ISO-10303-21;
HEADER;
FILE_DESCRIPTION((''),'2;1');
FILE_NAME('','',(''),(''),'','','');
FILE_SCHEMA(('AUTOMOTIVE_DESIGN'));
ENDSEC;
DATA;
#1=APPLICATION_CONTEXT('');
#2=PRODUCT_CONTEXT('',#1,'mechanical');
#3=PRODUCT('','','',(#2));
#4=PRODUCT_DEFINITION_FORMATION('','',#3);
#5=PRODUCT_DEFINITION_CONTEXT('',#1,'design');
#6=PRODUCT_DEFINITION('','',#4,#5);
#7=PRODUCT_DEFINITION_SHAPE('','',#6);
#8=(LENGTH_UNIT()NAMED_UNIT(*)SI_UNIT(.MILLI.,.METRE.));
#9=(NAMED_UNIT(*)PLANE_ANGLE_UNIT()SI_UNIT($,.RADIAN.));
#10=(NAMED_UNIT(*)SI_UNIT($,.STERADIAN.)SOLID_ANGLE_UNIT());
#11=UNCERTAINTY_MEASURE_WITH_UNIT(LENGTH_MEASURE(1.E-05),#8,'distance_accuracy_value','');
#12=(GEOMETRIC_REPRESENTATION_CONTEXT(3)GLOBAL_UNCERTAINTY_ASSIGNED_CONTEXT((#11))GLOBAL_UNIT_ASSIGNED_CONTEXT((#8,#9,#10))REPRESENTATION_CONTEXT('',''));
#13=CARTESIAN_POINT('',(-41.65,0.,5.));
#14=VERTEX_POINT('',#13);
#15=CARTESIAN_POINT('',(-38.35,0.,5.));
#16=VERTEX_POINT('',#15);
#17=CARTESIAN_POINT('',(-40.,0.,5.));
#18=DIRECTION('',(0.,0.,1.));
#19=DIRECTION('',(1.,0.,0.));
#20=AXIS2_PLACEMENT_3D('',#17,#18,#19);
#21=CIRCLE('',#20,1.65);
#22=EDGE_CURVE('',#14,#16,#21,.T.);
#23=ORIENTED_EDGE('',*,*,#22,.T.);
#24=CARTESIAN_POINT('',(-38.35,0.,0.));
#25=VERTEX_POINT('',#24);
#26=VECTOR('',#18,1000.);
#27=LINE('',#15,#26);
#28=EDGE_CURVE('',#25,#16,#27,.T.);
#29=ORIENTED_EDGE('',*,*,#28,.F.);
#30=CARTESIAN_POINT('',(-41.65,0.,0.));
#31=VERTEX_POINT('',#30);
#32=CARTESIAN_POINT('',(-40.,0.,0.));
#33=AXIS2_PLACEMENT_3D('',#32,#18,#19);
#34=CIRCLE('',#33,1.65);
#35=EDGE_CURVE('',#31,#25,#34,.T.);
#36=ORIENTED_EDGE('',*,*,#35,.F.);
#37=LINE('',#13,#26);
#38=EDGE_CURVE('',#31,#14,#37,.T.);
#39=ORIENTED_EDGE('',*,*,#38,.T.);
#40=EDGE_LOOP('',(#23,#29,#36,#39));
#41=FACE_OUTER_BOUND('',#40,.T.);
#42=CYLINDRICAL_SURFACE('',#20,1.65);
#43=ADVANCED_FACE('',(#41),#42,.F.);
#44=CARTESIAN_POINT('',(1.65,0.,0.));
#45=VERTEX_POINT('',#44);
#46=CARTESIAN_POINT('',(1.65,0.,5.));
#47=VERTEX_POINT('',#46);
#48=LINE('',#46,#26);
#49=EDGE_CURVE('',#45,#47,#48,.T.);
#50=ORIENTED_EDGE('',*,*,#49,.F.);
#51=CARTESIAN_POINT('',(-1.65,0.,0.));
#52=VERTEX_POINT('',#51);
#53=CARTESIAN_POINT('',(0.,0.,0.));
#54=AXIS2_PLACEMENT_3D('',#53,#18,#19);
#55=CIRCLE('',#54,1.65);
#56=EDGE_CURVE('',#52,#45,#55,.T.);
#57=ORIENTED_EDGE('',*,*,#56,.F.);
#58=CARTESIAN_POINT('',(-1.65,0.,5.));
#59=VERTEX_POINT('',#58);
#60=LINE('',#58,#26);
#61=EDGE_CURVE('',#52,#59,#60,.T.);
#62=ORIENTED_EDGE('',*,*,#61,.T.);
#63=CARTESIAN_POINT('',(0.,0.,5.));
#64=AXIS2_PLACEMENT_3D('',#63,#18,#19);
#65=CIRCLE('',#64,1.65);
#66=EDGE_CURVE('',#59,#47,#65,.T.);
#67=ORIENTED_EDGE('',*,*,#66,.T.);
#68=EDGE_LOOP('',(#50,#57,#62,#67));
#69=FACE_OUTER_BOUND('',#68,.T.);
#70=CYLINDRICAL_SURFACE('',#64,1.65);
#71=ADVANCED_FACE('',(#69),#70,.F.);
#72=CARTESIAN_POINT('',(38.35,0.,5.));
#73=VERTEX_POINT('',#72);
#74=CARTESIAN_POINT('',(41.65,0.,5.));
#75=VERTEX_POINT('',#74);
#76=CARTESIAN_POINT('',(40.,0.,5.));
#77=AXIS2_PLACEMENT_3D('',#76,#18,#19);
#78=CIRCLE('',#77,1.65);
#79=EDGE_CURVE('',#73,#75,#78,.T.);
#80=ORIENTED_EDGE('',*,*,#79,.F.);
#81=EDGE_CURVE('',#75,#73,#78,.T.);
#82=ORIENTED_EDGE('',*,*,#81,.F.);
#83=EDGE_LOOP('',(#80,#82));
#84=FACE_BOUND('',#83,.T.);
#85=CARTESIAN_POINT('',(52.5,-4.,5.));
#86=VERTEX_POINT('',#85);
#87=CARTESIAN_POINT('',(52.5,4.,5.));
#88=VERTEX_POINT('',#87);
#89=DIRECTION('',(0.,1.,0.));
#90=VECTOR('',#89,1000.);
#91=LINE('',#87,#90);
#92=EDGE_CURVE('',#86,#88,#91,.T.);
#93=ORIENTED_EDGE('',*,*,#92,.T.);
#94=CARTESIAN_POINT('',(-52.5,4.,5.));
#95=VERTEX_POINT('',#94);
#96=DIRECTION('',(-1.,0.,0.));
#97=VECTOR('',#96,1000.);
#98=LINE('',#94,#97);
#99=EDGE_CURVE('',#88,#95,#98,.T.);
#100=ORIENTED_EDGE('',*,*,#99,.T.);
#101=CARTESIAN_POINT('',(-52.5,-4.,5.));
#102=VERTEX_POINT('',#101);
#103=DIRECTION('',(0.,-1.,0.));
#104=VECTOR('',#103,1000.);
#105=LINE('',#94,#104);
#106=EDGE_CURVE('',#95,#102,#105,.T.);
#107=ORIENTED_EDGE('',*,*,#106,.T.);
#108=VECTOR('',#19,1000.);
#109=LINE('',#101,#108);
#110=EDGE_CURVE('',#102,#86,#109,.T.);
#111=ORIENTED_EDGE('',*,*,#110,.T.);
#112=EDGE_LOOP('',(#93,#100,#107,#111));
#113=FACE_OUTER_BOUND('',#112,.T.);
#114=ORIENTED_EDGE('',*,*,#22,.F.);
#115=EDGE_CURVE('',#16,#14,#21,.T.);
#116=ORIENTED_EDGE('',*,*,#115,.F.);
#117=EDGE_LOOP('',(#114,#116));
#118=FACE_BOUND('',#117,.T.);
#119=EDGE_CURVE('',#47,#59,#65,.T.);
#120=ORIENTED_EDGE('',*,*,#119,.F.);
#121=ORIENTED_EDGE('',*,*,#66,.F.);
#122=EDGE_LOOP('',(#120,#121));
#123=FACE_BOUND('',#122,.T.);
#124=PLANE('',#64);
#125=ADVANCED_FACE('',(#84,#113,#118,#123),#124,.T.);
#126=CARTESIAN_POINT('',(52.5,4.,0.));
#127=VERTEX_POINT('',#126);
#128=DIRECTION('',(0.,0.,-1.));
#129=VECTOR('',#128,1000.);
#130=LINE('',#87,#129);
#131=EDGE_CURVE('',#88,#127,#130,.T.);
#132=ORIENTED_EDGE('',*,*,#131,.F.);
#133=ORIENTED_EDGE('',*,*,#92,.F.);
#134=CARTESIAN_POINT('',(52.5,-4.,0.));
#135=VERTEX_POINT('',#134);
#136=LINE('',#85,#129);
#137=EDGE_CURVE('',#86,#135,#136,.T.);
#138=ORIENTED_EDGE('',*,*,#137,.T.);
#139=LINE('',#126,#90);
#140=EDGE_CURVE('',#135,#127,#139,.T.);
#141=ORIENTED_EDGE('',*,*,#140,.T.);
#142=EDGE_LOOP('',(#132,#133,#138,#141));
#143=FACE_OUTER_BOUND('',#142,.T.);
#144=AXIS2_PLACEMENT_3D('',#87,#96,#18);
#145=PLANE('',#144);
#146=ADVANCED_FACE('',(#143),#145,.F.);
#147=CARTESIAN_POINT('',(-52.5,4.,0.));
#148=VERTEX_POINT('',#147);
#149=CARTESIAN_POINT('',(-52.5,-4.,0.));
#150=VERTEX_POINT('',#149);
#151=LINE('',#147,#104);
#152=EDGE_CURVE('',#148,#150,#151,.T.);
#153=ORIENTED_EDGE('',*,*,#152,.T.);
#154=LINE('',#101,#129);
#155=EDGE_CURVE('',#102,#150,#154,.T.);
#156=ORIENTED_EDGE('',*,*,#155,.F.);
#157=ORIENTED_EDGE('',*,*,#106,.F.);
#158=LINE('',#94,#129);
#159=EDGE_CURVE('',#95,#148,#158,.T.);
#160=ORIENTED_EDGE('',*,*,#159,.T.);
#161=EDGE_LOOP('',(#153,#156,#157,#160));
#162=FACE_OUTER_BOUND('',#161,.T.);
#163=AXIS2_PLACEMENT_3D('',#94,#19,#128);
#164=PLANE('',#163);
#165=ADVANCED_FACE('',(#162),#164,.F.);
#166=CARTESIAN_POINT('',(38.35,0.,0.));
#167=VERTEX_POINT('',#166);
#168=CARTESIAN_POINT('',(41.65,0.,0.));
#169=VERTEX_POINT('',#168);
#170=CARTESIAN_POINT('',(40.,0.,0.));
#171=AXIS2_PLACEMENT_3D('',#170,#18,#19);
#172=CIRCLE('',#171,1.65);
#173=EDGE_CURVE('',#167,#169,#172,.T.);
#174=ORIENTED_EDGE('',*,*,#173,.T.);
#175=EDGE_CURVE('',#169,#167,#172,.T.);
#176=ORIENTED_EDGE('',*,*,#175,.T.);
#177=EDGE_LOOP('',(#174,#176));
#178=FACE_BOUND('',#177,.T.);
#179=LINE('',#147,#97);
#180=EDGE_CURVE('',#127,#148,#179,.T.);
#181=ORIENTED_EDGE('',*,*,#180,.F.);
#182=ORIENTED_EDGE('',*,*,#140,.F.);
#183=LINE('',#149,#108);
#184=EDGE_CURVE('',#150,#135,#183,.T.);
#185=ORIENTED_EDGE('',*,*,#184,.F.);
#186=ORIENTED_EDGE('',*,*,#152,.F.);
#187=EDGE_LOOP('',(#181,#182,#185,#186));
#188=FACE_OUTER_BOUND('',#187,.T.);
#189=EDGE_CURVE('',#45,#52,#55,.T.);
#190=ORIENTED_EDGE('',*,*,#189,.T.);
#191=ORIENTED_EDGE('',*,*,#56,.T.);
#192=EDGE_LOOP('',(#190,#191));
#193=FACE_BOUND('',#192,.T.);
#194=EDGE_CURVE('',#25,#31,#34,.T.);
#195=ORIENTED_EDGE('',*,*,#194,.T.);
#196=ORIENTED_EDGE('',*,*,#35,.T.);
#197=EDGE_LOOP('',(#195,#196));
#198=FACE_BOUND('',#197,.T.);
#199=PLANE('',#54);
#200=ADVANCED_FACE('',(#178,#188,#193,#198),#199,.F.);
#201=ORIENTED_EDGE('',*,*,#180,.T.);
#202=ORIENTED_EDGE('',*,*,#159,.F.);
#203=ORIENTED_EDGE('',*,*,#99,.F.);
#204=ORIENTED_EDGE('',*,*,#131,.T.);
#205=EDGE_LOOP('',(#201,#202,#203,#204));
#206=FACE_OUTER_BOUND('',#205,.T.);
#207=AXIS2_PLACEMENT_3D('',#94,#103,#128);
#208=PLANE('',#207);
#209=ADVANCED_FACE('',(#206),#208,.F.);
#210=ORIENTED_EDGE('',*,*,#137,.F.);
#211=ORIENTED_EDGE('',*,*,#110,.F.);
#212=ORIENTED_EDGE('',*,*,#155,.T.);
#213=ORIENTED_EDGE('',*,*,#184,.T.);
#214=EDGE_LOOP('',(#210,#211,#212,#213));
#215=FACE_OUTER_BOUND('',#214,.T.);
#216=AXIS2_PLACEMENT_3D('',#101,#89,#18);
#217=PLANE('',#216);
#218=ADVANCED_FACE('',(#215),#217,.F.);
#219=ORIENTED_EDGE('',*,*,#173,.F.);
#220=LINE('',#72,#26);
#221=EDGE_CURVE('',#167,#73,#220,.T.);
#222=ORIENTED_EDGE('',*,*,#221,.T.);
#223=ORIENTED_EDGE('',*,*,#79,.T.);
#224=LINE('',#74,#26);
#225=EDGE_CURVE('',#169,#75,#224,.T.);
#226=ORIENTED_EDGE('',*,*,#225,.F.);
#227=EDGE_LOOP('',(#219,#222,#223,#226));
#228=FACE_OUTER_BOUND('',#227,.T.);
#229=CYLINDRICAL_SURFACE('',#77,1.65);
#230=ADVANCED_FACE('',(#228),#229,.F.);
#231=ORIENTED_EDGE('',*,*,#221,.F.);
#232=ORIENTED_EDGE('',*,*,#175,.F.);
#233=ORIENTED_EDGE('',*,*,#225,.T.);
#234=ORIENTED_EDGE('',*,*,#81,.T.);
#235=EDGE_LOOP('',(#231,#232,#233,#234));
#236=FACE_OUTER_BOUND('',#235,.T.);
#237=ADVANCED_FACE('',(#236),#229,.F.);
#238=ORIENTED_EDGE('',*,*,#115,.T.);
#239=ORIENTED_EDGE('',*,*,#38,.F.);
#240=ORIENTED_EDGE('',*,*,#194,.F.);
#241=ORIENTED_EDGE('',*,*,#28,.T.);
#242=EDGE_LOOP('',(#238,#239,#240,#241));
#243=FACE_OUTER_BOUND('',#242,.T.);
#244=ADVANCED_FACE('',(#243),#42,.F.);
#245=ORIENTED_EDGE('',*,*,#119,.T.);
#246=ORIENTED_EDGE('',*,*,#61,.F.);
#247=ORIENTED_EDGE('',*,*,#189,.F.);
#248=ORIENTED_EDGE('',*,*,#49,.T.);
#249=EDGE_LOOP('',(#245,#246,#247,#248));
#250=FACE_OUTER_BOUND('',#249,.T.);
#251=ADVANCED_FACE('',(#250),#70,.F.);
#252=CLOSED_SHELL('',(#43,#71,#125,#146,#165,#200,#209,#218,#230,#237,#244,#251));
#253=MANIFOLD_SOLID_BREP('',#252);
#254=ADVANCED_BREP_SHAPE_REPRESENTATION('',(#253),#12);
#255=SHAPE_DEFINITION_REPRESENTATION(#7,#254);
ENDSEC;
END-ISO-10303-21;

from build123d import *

# Parameters (mm, degrees)
SKETCH1_W           = 105
SKETCH1_H           = 8
BOSS_EXTRUDE1_DEPTH = 5
M4_TAPPED_HOLE2_D   = 3.3


with BuildPart() as part:
    # Sketch1 → Boss-Extrude1 (new body)
    with BuildSketch(Plane.XY):
        Rectangle(SKETCH1_W, SKETCH1_H)
    extrude(amount=BOSS_EXTRUDE1_DEPTH)

    # M4 Tapped Hole2 (through all)
    with Locations(Plane.XY.offset(5)):
        with Locations((-40, 0), (0, 0), (40, 0)):
            Hole(M4_TAPPED_HOLE2_D / 2)


solid = part.part
